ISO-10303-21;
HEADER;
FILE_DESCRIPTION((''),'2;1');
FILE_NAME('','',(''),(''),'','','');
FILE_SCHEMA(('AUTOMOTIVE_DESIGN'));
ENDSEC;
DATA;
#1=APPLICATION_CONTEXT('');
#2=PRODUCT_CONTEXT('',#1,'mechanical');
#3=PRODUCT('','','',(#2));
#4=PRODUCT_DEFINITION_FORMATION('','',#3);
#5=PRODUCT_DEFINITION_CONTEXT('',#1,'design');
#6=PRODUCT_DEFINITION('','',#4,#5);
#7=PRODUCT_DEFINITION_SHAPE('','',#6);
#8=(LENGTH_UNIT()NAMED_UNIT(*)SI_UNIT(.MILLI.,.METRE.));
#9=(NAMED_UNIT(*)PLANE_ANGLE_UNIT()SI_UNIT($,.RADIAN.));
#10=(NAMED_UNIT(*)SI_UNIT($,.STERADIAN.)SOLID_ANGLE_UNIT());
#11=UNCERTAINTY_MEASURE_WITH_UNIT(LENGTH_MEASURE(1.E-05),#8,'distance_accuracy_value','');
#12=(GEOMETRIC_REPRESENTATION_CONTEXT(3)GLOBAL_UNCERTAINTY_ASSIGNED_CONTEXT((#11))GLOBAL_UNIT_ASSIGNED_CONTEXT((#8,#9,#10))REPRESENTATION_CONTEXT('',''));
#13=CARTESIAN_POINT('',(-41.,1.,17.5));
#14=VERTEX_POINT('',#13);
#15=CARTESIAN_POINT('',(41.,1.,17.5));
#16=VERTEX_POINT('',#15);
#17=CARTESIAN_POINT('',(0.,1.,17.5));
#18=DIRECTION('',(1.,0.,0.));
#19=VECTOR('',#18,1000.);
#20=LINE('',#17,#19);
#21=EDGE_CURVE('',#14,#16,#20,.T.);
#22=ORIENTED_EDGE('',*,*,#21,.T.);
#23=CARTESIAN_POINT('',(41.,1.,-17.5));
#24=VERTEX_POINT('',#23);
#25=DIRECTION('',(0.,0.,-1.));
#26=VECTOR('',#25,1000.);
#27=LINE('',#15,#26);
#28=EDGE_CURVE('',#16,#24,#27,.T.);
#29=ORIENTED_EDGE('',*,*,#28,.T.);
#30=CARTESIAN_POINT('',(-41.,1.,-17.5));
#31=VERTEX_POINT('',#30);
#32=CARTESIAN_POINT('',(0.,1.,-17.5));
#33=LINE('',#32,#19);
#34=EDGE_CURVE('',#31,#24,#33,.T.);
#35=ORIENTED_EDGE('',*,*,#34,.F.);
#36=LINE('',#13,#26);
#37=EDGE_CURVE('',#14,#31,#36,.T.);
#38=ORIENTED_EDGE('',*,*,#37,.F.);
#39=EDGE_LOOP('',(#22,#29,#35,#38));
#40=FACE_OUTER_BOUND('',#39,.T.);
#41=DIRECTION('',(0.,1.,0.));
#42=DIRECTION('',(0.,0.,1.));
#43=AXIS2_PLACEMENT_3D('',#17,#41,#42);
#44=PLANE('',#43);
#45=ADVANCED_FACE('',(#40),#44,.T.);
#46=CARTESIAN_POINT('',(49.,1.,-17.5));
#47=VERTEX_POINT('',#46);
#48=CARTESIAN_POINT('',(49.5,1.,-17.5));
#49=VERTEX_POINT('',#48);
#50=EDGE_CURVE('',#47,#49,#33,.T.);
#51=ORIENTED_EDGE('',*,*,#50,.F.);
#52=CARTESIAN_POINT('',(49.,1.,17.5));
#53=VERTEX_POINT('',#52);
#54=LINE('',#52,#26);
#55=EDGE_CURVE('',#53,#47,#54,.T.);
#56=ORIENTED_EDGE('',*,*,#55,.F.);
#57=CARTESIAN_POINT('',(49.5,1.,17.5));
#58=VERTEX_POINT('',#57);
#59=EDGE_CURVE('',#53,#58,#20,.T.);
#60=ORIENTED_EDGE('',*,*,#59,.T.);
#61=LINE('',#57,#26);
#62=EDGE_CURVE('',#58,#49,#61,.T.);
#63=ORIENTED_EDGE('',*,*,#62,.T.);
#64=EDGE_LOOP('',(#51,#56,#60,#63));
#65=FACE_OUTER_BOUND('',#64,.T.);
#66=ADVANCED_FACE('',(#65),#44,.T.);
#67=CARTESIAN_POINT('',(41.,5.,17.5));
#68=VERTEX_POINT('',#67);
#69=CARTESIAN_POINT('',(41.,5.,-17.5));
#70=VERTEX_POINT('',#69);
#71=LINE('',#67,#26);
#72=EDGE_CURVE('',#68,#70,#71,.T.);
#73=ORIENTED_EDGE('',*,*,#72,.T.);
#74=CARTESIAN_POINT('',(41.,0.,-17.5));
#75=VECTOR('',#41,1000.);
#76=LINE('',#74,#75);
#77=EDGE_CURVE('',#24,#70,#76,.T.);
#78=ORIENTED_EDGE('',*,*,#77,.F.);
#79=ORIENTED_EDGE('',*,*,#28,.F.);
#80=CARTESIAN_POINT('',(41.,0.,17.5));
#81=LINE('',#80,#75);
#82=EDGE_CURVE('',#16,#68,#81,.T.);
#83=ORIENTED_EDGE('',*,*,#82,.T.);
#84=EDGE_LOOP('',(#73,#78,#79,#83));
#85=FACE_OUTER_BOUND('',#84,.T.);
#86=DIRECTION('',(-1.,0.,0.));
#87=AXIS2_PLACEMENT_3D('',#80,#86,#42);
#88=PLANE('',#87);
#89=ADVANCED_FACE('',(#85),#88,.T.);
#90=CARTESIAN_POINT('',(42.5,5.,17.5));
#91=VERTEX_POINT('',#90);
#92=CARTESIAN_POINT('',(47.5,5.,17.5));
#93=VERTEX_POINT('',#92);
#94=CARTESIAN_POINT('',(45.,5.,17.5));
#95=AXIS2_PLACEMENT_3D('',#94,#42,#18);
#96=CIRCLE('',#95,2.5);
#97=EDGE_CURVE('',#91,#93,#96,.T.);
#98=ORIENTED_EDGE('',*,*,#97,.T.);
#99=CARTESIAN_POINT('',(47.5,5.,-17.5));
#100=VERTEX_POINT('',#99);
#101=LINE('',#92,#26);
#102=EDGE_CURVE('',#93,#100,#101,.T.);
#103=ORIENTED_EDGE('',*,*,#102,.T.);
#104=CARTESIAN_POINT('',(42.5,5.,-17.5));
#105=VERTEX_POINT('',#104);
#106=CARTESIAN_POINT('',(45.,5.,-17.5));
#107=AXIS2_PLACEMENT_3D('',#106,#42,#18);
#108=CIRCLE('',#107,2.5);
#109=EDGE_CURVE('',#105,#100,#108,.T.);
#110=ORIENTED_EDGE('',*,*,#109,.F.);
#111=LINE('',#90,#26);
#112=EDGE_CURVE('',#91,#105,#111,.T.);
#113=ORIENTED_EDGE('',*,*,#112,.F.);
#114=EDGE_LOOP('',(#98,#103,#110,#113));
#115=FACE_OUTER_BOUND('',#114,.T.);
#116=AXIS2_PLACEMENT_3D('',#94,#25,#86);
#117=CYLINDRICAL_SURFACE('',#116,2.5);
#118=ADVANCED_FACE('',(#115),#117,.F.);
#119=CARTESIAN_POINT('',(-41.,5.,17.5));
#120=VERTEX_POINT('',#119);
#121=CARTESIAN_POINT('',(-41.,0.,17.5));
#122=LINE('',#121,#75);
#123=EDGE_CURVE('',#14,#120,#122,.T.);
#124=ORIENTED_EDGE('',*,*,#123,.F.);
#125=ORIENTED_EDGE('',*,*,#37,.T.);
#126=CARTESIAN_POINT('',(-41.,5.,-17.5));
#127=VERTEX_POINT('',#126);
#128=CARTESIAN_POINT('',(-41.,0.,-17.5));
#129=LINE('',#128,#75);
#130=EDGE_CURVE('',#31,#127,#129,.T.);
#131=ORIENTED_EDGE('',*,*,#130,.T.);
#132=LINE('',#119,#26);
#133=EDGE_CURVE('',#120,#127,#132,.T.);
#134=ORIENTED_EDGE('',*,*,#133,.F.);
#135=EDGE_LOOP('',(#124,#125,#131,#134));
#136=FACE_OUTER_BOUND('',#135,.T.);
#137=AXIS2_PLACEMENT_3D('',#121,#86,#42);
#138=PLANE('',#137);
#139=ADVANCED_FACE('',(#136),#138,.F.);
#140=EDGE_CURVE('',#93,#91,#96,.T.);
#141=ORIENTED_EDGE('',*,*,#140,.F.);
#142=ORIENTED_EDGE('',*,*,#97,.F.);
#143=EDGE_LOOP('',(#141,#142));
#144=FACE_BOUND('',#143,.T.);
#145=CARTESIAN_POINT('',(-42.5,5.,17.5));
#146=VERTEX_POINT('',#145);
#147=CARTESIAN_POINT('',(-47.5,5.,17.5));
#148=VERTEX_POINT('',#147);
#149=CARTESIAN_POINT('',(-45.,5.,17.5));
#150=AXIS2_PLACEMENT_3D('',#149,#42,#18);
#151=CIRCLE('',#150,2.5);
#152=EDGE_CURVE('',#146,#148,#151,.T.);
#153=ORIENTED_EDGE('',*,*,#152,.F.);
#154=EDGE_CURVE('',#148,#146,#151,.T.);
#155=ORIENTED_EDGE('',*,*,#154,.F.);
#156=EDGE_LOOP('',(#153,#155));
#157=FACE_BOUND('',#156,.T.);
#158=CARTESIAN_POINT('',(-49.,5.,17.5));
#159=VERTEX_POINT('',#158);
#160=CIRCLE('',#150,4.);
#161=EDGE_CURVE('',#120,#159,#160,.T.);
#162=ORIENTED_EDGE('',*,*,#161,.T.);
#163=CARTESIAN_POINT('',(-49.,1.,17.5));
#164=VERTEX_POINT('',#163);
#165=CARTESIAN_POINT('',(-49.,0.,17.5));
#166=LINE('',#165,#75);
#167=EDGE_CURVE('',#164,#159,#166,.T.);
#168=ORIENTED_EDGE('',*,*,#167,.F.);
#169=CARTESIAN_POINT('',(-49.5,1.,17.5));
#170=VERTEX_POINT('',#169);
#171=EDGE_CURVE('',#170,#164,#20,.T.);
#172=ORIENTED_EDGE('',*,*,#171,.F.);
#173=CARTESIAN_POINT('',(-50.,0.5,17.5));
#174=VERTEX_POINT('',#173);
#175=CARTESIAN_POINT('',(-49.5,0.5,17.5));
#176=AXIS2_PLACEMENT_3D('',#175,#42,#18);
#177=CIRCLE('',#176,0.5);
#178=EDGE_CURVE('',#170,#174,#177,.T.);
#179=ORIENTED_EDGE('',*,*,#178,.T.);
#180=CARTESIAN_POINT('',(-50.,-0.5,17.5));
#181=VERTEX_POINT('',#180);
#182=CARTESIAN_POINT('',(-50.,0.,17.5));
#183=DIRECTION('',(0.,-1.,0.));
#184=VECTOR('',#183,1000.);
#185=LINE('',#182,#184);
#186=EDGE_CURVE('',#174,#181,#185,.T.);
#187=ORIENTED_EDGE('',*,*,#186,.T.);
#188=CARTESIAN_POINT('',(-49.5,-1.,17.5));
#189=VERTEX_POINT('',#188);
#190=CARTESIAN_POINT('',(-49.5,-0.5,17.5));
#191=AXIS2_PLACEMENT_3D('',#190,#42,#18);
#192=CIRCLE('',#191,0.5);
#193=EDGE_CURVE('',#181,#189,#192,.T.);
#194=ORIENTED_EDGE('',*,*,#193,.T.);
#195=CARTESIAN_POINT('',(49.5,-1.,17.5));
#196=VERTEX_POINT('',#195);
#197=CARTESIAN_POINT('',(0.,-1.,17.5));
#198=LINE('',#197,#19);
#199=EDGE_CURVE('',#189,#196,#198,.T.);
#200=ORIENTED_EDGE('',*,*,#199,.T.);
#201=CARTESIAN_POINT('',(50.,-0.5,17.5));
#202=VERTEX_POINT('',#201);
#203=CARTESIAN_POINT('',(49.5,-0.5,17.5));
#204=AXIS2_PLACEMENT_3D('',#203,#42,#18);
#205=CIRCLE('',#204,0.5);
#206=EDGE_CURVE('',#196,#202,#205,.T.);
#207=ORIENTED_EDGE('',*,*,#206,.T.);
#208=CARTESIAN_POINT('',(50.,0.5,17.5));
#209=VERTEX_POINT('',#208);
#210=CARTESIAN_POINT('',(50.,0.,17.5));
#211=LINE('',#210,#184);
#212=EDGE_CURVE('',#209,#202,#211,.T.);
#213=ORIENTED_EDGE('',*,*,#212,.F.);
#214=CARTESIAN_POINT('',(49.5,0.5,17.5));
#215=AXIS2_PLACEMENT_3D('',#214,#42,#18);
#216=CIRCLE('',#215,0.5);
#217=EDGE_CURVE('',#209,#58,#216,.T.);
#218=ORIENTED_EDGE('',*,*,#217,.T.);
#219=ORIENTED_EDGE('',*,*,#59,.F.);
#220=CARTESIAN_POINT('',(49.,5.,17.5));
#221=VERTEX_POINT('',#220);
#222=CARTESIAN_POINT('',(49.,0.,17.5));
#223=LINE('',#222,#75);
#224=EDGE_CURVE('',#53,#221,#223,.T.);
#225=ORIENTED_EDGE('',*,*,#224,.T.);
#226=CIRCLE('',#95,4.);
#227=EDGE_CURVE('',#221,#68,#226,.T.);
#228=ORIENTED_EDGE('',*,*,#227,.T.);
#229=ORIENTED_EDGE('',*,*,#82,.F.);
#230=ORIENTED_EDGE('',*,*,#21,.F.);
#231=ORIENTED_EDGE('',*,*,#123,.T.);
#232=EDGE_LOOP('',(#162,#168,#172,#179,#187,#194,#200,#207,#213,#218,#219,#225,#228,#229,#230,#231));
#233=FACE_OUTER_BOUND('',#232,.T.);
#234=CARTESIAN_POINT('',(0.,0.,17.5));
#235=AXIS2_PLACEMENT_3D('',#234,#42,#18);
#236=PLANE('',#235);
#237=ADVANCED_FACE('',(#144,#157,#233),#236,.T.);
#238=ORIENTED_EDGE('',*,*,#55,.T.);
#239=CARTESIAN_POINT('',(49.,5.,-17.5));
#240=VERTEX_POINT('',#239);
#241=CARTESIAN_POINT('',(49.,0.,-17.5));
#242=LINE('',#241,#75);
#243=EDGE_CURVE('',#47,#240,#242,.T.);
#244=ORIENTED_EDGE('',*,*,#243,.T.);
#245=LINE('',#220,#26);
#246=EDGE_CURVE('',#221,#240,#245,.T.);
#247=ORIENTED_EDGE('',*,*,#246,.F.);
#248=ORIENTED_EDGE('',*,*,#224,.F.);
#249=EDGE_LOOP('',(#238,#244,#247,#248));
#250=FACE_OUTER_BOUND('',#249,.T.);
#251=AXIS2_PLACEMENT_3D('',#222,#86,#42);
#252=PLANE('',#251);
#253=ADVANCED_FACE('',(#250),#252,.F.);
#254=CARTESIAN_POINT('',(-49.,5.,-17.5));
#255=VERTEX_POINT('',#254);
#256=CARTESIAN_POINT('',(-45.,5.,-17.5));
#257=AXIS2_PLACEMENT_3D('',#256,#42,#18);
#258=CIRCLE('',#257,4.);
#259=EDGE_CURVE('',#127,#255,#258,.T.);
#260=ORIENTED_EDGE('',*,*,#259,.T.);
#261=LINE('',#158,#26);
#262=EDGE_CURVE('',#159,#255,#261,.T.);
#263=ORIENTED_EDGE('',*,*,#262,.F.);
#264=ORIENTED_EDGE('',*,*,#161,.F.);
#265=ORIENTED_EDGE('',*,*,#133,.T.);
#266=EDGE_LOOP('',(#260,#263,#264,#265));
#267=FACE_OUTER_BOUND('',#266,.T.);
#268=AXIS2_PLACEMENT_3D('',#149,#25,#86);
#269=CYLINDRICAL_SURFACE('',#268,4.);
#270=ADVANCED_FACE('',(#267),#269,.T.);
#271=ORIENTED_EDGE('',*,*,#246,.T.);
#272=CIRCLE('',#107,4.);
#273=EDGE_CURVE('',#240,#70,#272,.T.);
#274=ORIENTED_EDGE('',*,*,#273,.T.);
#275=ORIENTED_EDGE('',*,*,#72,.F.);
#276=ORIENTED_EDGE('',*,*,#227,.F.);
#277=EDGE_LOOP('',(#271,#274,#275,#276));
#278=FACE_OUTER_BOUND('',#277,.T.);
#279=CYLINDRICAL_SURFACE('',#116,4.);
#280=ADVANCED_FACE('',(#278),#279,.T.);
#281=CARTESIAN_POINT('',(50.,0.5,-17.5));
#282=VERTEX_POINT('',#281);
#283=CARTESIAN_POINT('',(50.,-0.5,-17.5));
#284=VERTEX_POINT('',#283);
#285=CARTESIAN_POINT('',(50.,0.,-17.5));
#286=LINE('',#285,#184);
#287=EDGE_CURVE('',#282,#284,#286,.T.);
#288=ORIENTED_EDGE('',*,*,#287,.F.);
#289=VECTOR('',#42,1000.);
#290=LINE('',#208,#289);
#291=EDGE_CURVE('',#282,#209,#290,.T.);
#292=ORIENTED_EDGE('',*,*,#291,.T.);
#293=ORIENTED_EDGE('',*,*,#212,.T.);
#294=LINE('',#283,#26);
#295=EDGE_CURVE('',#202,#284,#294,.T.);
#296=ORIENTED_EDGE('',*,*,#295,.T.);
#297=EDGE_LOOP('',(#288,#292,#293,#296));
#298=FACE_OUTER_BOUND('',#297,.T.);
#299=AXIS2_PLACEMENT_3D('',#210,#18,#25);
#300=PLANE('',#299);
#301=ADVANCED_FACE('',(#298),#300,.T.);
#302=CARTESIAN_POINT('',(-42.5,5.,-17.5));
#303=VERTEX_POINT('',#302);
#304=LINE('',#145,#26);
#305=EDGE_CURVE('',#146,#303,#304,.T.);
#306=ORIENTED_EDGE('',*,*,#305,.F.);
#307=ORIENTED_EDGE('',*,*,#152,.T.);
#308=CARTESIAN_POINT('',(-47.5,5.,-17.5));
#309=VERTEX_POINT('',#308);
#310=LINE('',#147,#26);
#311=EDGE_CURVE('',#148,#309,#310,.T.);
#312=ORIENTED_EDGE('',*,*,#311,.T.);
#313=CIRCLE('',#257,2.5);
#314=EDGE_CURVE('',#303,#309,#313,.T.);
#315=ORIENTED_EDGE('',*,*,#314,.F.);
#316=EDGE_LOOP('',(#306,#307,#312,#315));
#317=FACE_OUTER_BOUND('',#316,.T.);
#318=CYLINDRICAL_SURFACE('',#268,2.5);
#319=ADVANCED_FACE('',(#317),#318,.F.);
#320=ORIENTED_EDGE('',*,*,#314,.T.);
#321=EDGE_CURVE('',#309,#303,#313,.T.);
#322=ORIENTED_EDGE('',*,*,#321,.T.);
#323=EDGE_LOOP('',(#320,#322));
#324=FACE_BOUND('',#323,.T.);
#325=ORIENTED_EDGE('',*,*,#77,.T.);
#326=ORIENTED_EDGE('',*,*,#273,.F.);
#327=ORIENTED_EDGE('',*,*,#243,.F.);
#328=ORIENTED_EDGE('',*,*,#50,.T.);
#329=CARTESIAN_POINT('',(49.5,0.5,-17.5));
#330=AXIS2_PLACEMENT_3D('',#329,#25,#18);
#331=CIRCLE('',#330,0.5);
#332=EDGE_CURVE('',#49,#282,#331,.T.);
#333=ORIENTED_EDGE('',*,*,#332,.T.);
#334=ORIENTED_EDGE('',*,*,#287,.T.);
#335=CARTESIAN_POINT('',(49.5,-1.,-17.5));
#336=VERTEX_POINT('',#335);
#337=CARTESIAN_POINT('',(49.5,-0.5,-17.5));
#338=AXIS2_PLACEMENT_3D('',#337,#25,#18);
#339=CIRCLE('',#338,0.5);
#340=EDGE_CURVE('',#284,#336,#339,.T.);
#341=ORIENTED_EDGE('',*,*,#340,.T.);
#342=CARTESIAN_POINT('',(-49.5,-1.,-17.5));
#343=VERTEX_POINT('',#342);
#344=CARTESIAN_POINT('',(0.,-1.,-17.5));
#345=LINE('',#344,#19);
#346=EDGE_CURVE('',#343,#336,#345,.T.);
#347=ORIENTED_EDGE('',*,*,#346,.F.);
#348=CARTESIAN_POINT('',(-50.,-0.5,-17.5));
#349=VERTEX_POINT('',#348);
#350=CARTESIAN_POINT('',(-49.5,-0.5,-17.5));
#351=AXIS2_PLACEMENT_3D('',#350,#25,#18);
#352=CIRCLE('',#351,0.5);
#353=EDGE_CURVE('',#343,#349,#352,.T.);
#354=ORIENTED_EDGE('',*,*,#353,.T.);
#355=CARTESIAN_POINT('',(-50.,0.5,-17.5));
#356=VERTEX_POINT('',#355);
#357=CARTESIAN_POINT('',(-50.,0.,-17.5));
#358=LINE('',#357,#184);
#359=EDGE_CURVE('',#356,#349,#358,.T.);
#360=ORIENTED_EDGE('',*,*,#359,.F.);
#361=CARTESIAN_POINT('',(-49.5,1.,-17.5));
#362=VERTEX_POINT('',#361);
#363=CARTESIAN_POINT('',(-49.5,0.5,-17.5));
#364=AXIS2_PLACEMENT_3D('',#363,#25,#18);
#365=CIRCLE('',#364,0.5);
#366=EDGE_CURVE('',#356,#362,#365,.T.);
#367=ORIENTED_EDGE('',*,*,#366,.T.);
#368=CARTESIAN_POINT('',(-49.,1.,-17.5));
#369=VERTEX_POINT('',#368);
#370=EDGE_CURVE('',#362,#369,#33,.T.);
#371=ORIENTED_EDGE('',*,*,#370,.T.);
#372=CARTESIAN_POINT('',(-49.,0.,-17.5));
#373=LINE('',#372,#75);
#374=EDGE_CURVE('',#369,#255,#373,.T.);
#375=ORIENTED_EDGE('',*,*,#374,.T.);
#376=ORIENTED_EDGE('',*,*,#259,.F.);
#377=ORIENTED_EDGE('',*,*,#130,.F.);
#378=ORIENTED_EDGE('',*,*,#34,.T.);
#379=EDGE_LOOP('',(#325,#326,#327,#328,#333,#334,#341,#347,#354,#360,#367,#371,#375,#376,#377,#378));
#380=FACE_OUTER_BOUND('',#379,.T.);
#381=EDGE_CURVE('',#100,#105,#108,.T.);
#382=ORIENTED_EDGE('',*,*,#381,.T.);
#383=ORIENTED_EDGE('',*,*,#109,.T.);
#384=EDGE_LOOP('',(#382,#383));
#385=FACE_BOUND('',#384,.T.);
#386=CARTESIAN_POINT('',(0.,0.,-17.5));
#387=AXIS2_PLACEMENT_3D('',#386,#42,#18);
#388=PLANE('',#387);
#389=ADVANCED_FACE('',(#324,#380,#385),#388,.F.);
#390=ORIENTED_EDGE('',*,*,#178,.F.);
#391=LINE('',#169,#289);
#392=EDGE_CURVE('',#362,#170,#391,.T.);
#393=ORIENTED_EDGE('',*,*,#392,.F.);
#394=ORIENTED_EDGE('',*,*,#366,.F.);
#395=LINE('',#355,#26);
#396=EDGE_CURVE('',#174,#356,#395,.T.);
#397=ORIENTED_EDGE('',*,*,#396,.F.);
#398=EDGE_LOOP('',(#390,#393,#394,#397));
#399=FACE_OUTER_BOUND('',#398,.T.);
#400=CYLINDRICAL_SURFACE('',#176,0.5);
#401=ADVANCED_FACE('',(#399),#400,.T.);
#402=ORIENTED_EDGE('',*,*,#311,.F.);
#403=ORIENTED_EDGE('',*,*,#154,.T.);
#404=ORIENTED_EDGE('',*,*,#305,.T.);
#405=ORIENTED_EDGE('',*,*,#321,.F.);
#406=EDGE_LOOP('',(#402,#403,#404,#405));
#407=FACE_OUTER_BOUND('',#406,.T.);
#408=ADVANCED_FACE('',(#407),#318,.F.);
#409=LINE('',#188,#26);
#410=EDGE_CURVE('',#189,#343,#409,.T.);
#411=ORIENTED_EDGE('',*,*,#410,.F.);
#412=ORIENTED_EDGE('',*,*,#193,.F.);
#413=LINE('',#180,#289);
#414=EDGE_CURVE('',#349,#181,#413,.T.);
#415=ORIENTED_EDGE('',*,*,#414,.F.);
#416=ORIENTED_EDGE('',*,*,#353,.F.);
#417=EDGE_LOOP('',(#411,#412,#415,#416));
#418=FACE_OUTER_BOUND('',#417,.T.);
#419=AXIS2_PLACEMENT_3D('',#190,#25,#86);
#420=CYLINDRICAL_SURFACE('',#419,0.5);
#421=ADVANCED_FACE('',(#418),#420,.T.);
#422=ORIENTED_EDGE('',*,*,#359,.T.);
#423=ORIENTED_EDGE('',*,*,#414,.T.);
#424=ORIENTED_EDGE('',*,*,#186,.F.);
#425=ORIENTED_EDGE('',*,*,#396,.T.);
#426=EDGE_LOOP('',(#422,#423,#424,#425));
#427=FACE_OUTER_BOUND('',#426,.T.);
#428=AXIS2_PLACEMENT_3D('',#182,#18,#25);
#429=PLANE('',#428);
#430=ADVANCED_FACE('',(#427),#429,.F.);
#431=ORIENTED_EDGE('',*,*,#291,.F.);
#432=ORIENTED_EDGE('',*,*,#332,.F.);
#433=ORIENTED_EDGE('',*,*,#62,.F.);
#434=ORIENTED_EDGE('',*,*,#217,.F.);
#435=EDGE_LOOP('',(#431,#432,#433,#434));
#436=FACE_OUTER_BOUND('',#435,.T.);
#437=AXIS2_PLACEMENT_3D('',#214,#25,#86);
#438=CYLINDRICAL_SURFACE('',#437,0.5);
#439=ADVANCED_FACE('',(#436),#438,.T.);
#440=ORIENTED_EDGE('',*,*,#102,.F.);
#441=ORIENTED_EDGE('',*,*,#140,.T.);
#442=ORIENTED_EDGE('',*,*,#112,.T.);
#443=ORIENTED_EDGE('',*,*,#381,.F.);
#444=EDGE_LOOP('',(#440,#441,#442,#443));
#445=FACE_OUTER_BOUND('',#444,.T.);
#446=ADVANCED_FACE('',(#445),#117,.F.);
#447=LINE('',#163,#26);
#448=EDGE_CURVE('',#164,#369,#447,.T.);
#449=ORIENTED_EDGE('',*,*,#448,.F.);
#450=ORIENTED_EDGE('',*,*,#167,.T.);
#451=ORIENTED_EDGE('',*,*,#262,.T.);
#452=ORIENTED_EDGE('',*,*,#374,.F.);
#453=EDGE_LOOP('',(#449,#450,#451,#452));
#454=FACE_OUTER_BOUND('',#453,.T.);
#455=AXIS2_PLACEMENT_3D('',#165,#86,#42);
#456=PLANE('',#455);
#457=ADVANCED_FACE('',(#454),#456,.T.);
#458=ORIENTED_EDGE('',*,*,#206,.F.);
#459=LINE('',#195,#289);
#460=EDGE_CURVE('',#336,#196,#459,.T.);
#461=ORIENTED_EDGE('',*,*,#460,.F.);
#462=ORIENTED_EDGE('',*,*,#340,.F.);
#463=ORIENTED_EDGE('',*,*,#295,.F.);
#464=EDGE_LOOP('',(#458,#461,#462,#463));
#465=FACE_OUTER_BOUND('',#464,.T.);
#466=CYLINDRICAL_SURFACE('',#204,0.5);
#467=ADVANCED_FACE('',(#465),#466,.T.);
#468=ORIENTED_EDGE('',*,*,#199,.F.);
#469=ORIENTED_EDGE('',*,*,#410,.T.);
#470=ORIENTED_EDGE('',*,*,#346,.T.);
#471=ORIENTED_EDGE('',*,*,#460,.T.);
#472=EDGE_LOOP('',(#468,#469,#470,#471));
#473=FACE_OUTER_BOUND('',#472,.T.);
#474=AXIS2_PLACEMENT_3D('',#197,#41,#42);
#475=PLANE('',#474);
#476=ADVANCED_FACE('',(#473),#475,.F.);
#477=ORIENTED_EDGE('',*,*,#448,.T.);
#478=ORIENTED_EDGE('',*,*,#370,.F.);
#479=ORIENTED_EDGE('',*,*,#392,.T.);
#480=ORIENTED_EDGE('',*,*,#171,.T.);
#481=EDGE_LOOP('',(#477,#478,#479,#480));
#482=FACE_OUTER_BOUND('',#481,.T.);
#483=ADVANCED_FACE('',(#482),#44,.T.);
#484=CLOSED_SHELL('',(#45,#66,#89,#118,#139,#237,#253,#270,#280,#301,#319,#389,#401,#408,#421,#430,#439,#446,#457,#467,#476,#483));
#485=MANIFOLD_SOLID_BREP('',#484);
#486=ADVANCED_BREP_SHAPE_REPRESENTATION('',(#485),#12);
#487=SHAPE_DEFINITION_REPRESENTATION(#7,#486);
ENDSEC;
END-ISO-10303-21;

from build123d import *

# Parameters (mm, degrees)
ROLLED_EDGE_PLATE_PROFILE_R   = 2.5
ROLLED_EDGE_PLATE_PROFILE_W   = 82
ROLLED_EDGE_PLATE_PROFILE_H   = 2
ROLLED_EDGE_PLATE_PROFILE_W_2 = 1
ROLLED_EDGE_PLATE_PROFILE_W_3 = 8
PLATE_EXTRUDE_35MM_DEPTH      = 17.5
EDGE_FILLETS_R0_5_R           = 0.5


with BuildPart() as part:
    # Rolled Edge Plate Profile → Plate Extrude 35mm (new, symmetric)
    # profile 1 of 7: a face of its own
    with BuildSketch(Plane.XY):
        with BuildLine():
            Line((41, 5), (41, 1))
            Line((41, 1), (49, 1))
            Line((49, 1), (49, 5))
            ThreePointArc((49, 5), (45, 9), (41, 5))
        make_face()
        with Locations((45, 5)):
            Circle(ROLLED_EDGE_PLATE_PROFILE_R, mode=Mode.SUBTRACT)
    # profile 2 of 7: a face of its own
    with BuildSketch(Plane.XY):
        Rectangle(ROLLED_EDGE_PLATE_PROFILE_W, ROLLED_EDGE_PLATE_PROFILE_H)
    # profile 3 of 7: a face of its own
    with BuildSketch(Plane.XY):
        with Locations((49.5, 0)):
            Rectangle(ROLLED_EDGE_PLATE_PROFILE_W_2, ROLLED_EDGE_PLATE_PROFILE_H)
    # profile 4 of 7: a face of its own
    with BuildSketch(Plane.XY):
        with Locations((45, 0)):
            Rectangle(ROLLED_EDGE_PLATE_PROFILE_W_3, ROLLED_EDGE_PLATE_PROFILE_H)
    # profile 5 of 7: a face of its own
    with BuildSketch(Plane.XY):
        with Locations((-45, 0)):
            Rectangle(ROLLED_EDGE_PLATE_PROFILE_W_3, ROLLED_EDGE_PLATE_PROFILE_H)
    # profile 6 of 7: a face of its own
    with BuildSketch(Plane.XY):
        with Locations((-49.5, 0)):
            Rectangle(ROLLED_EDGE_PLATE_PROFILE_W_2, ROLLED_EDGE_PLATE_PROFILE_H)
    # profile 7 of 7: a face of its own
    with BuildSketch(Plane.XY):
        with BuildLine():
            Line((-49, 5), (-49, 1))
            Line((-49, 1), (-41, 1))
            Line((-41, 1), (-41, 5))
            ThreePointArc((-41, 5), (-45, 9), (-49, 5))
        make_face()
        with Locations((-45, 5)):
            Circle(ROLLED_EDGE_PLATE_PROFILE_R, mode=Mode.SUBTRACT)
    extrude(amount=PLATE_EXTRUDE_35MM_DEPTH, both=True)

    # Edge Fillets R0.5
    edge_fillets_r0_5_edges = [part.edges().sort_by_distance(p)[0] for p in [
        (50, 1, 0),
        (50, -1, 0),
        (-50, -1, 0),
        (-50, 1, 0),
    ]]
    fillet(edge_fillets_r0_5_edges, radius=EDGE_FILLETS_R0_5_R)


solid = part.part
